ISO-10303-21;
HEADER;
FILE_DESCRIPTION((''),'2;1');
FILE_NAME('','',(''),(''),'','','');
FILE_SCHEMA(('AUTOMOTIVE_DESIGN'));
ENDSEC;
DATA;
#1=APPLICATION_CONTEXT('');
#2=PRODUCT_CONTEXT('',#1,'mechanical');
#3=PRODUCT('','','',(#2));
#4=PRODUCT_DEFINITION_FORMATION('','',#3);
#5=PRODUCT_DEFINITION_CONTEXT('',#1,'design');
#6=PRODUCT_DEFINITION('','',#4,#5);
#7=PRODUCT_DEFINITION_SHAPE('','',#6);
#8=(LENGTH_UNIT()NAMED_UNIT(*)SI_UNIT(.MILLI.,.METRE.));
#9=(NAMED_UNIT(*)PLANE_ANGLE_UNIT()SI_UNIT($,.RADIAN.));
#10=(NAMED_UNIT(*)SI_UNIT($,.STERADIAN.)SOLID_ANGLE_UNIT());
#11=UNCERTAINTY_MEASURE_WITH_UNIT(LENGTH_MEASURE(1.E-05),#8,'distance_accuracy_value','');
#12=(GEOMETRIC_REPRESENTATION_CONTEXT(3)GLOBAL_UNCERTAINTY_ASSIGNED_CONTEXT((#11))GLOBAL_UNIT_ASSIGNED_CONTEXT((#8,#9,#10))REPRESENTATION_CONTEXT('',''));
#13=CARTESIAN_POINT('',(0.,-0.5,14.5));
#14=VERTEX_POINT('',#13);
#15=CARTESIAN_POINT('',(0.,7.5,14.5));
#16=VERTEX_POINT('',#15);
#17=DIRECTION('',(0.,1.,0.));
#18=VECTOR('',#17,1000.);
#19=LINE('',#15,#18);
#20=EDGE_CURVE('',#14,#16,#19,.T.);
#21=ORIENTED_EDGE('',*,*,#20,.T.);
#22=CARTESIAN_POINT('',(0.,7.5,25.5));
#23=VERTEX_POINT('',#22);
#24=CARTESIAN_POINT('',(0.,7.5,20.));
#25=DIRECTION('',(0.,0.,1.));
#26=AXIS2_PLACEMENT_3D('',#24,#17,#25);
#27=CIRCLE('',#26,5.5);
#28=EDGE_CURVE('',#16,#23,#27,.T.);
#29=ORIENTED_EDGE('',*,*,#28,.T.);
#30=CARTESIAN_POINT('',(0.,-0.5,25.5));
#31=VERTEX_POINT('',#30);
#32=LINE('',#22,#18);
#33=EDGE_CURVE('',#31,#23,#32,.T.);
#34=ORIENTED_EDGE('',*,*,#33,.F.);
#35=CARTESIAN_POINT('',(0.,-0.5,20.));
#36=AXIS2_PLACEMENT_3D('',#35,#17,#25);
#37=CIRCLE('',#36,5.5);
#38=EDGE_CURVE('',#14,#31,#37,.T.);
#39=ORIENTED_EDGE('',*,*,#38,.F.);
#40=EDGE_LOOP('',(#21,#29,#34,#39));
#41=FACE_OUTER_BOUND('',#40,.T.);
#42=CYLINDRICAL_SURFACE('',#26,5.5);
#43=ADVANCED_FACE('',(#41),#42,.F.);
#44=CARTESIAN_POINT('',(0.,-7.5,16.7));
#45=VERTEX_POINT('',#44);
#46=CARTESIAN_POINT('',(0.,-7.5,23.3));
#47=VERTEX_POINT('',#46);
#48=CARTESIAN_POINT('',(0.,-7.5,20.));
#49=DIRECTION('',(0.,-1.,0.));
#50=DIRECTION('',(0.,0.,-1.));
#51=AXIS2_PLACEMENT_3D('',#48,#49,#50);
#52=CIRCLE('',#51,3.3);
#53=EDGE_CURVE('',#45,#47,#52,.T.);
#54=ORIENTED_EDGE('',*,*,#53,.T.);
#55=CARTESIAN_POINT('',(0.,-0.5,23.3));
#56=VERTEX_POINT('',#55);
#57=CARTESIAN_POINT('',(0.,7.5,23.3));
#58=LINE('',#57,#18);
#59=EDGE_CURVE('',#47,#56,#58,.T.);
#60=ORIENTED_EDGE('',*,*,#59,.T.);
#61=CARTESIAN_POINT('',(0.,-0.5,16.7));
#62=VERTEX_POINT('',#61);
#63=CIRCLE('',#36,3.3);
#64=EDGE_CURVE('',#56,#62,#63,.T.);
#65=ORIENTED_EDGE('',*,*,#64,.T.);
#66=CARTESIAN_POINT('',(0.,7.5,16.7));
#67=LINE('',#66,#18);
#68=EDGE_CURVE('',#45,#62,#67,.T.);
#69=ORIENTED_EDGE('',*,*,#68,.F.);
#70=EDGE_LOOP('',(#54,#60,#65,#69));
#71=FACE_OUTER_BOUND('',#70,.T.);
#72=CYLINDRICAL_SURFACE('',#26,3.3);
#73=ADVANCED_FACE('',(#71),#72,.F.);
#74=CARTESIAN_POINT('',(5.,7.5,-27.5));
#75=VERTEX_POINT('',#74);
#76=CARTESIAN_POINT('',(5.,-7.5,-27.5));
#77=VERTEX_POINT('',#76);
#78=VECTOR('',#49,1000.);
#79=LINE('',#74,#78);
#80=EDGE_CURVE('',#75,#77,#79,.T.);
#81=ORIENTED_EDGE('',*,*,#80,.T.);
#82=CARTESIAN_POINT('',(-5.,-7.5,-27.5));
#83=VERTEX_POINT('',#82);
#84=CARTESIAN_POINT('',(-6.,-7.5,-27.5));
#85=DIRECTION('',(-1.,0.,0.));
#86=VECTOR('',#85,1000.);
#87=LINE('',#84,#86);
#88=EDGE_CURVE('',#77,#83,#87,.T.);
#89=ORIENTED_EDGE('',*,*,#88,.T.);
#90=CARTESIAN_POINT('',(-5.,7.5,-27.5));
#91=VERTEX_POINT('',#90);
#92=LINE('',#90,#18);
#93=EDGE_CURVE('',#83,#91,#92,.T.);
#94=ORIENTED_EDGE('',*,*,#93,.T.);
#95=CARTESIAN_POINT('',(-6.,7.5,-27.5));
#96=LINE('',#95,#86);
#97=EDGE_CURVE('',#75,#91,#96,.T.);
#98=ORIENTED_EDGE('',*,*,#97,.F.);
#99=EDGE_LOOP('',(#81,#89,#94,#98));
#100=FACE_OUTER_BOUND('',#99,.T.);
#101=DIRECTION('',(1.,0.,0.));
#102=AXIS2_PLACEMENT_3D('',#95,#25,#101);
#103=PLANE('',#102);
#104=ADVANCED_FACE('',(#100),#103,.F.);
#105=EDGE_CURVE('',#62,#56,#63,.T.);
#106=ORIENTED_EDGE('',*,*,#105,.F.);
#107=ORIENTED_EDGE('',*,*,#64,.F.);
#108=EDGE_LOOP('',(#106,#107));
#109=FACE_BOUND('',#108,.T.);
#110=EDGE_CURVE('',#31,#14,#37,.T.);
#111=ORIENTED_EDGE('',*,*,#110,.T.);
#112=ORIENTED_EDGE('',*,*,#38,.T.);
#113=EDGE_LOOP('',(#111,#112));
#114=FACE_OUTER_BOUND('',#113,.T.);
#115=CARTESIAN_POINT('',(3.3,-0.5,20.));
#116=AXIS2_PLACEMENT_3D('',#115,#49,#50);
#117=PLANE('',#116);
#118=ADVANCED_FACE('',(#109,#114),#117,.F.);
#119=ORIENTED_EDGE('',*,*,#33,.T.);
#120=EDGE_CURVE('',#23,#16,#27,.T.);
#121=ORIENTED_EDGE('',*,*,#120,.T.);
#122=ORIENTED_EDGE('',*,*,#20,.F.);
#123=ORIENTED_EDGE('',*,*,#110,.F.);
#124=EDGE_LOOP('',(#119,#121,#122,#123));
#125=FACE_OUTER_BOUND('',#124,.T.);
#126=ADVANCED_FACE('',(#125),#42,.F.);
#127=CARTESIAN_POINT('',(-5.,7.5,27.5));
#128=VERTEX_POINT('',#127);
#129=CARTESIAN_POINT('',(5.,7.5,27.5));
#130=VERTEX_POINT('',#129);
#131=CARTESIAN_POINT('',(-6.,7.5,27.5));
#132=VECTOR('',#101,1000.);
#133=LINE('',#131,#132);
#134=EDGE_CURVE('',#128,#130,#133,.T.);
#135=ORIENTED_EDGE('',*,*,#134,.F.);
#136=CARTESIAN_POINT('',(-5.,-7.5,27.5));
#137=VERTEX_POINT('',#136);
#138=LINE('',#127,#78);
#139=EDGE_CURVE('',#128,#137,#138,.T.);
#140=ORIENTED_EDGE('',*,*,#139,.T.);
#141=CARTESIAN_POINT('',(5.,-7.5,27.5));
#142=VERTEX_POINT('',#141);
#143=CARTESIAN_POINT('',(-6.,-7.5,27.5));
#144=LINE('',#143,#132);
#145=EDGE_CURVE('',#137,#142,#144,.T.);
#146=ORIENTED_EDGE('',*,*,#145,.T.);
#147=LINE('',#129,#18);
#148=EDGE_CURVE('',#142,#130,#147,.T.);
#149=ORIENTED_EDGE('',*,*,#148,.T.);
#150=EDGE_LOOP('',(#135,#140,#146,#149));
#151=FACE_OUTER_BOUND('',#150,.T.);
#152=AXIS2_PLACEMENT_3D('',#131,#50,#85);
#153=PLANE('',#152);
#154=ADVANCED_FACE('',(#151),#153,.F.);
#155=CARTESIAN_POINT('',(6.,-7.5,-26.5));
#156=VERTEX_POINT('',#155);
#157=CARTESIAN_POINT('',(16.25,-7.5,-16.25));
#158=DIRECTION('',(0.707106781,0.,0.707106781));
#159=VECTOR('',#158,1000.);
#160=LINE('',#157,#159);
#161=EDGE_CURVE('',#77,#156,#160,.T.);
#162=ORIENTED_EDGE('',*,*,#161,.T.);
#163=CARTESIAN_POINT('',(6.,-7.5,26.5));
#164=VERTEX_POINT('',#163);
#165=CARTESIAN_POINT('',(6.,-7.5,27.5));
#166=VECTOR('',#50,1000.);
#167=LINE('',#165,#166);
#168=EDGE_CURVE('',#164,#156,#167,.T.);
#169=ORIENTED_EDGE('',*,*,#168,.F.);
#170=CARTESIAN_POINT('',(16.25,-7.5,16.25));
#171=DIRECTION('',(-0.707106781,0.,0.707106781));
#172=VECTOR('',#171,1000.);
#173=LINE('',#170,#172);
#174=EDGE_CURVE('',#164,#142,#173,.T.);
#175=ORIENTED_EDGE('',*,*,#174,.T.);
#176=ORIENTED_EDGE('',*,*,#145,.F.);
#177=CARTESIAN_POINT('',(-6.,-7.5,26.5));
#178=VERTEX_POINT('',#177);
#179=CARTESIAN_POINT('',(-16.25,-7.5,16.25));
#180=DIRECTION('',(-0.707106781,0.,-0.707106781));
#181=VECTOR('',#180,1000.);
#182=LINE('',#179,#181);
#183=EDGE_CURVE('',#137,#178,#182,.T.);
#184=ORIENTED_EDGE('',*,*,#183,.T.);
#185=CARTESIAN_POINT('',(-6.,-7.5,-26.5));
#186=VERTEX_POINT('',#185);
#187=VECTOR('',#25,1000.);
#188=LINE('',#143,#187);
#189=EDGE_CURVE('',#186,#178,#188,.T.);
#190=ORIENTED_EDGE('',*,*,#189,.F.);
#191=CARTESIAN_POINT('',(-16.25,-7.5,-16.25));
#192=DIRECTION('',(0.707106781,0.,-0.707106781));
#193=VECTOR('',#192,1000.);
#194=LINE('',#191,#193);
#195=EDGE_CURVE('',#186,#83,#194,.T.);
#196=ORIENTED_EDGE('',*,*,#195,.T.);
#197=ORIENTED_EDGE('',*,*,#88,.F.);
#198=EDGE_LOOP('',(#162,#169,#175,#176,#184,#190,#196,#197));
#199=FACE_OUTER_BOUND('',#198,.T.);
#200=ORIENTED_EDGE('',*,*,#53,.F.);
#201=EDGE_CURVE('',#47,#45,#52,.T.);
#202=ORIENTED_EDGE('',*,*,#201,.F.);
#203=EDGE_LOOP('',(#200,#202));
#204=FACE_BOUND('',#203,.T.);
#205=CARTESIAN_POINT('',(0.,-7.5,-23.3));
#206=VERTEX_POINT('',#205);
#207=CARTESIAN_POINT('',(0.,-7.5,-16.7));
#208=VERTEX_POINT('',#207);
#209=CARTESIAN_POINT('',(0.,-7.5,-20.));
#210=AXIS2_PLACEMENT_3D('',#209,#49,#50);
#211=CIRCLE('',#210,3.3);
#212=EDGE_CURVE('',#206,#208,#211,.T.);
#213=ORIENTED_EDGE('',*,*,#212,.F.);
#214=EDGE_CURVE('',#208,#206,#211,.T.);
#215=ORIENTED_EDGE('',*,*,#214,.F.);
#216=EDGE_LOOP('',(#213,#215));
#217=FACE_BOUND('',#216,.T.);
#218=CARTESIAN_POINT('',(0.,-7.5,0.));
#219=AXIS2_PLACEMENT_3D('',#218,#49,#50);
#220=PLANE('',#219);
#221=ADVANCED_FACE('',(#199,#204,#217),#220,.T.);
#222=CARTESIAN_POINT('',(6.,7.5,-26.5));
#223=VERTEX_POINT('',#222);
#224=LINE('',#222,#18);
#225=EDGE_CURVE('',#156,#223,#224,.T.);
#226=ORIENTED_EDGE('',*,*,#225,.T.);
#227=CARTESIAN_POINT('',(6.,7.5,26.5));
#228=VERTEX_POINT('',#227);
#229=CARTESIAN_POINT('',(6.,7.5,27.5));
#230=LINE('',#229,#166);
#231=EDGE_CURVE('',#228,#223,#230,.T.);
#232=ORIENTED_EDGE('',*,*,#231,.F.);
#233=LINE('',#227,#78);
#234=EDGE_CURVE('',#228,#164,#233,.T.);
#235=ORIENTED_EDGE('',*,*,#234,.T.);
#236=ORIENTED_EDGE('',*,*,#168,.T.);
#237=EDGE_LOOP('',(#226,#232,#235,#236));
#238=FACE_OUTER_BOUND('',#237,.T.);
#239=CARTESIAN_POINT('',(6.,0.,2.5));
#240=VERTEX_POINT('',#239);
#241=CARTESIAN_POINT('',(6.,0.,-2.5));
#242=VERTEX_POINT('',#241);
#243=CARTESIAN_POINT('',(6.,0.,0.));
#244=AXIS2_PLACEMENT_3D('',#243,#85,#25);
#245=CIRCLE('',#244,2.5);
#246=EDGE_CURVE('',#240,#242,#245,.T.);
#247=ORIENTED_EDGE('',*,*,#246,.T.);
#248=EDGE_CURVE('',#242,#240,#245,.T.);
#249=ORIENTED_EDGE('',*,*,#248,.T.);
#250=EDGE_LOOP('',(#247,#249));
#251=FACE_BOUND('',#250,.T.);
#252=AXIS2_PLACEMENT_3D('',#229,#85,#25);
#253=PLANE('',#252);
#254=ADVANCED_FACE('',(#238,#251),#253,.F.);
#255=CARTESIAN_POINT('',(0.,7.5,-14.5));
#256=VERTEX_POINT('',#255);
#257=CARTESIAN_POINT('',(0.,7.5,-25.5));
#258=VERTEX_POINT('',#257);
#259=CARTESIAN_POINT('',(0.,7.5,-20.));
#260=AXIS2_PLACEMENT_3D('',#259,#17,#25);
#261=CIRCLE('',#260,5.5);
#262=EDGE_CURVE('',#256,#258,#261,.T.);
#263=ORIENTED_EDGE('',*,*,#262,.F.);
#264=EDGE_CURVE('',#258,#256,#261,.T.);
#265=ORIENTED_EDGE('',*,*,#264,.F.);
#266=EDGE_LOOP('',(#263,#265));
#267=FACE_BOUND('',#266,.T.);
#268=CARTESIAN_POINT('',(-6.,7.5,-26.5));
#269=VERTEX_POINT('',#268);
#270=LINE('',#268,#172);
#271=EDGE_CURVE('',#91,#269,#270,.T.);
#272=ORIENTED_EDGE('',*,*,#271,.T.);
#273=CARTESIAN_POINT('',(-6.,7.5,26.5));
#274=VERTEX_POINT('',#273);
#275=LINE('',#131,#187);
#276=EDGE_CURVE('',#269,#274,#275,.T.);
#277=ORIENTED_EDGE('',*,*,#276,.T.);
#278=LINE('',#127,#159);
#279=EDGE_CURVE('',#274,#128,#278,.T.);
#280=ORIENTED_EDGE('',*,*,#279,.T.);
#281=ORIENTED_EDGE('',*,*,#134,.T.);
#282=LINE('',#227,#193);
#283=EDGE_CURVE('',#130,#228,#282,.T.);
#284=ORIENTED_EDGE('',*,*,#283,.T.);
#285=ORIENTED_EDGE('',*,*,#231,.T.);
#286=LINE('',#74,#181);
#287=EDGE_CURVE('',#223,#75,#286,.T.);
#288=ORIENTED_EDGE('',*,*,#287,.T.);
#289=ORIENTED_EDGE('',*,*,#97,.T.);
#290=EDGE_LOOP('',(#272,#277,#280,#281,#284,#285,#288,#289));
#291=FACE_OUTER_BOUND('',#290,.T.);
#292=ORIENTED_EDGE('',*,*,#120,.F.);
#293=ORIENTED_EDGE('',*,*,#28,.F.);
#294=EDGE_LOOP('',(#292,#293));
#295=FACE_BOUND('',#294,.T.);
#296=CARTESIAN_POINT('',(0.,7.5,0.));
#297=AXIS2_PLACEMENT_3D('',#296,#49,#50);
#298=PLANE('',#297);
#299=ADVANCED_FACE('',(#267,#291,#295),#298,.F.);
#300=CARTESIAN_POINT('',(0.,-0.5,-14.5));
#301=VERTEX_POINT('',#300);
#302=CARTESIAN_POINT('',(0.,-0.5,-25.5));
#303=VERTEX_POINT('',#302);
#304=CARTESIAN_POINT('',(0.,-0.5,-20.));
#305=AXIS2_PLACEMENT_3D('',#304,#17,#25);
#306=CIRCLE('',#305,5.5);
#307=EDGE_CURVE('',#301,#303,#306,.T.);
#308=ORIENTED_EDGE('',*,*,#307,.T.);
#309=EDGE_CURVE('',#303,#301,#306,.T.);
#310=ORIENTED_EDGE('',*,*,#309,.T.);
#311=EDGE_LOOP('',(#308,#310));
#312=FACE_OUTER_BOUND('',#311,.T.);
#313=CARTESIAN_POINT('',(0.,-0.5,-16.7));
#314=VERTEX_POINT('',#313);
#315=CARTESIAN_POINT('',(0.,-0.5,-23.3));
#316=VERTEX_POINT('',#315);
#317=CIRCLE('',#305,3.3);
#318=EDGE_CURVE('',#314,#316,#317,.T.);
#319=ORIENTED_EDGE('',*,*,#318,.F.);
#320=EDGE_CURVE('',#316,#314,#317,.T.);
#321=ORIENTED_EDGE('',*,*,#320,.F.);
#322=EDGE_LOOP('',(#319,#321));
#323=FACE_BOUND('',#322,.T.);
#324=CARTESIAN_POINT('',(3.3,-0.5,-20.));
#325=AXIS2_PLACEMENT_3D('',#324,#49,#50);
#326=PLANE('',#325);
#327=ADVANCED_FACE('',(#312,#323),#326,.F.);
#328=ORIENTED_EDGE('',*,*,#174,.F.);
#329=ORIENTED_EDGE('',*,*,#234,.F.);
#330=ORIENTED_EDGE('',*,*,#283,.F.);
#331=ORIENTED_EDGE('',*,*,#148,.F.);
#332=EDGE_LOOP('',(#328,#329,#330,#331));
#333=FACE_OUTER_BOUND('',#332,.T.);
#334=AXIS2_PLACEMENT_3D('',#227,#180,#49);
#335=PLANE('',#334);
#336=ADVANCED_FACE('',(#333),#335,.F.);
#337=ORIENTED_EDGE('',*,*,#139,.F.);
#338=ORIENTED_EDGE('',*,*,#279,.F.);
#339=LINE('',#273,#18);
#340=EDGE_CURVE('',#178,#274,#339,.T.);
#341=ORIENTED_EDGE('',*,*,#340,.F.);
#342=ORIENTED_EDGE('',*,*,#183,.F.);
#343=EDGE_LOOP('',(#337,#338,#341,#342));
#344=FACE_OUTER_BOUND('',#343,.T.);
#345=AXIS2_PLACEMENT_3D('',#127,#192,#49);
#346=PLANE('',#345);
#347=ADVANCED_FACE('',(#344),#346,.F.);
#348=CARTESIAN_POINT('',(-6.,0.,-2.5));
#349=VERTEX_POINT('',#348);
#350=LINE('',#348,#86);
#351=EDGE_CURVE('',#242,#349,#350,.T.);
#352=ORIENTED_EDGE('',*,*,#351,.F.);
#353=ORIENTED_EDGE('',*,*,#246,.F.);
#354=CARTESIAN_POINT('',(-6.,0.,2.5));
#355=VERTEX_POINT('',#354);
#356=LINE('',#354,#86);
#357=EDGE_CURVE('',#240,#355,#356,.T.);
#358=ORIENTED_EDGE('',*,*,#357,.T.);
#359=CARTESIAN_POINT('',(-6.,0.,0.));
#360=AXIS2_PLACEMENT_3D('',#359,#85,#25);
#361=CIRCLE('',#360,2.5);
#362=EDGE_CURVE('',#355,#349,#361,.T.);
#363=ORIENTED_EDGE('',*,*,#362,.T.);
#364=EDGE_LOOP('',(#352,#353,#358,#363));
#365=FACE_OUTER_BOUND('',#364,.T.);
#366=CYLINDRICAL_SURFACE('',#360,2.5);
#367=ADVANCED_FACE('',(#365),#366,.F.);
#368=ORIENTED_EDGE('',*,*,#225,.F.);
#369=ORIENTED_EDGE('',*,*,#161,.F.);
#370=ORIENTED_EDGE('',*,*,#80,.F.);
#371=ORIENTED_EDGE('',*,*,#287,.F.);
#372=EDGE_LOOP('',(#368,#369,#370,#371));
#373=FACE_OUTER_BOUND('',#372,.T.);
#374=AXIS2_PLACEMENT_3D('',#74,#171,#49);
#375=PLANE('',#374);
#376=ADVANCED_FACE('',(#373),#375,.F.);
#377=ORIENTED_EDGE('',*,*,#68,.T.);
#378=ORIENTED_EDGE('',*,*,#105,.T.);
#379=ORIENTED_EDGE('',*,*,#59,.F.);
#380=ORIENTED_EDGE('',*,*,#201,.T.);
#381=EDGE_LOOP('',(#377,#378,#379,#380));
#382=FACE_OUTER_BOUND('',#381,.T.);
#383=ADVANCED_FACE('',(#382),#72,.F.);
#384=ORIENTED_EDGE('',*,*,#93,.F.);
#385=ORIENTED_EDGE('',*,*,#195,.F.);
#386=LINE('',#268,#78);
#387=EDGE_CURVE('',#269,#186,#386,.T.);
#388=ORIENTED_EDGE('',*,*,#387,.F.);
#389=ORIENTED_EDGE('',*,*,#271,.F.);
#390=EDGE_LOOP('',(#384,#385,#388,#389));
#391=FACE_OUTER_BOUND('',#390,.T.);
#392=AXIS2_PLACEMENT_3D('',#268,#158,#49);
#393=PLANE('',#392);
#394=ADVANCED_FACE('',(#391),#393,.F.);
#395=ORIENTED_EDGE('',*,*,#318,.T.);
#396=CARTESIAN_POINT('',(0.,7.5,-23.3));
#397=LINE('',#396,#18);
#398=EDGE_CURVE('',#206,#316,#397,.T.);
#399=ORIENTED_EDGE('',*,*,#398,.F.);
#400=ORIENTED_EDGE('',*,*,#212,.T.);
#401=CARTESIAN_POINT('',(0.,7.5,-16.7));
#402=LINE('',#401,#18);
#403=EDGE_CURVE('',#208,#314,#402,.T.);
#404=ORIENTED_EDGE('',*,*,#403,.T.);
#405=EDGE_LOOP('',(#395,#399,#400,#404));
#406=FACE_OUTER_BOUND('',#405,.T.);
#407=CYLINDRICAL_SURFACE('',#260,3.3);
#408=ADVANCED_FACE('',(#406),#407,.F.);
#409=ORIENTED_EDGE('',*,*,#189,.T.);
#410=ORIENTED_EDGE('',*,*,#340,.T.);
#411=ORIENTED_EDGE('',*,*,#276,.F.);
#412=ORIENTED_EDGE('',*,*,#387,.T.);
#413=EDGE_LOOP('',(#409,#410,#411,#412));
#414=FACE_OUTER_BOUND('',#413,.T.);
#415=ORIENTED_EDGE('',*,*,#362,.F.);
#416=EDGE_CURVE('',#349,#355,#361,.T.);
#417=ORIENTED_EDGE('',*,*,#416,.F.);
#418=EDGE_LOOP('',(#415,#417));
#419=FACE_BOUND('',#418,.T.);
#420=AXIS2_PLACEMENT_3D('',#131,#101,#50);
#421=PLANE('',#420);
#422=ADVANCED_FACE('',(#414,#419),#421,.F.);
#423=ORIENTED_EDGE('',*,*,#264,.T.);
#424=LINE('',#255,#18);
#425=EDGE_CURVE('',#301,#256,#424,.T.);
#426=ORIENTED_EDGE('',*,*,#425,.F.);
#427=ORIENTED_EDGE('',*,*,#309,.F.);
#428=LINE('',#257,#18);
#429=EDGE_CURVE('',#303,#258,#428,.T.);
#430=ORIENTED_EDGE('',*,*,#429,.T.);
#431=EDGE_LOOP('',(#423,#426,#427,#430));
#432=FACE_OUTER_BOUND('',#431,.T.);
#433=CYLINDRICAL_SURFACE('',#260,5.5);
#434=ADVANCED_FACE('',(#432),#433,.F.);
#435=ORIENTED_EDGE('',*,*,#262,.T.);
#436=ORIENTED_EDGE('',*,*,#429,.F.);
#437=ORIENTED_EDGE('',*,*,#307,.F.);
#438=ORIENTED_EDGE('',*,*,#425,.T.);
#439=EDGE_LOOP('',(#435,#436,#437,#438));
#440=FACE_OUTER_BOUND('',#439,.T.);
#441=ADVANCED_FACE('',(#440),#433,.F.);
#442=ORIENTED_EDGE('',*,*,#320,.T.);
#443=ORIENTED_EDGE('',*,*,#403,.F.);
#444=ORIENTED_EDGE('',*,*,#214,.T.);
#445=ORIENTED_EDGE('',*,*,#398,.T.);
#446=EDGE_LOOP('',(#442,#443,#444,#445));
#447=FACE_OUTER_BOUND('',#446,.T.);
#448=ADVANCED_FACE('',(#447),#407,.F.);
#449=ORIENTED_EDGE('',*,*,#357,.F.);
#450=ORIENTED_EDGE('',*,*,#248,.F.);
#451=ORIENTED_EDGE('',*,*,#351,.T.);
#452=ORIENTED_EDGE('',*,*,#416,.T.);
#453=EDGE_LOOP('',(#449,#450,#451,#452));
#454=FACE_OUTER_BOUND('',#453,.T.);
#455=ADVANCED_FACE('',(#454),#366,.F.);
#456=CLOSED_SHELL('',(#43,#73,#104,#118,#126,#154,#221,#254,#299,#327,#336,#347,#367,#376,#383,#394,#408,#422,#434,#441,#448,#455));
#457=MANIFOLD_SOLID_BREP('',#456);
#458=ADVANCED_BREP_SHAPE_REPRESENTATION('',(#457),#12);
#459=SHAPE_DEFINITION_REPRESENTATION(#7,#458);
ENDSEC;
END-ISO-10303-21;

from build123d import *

# Parameters (mm, degrees)
SKETCH_1_W                   = 12
SKETCH_1_H                   = 55
EXTRUDE_1_DEPTH              = 7.5
CHAMFER_1_SIZE               = 1
HOLE_WIZARD_M6_1_D           = 6.6
HOLE_WIZARD_M6_1_CBORE_D     = 11
HOLE_WIZARD_M6_1_CBORE_DEPTH = 8
HOLE_WIZARD_M6_1_2_D         = 5


with BuildPart() as part:
    # 草图1 → 凸台-拉伸1 (new, symmetric)
    with BuildSketch(Plane(origin=(0, 0, 0), x_dir=(1, 0, 0), z_dir=(0, 1, 0))):
        Rectangle(SKETCH_1_W, SKETCH_1_H)
    extrude(amount=EXTRUDE_1_DEPTH, both=True)

    # 倒角1
    chamfer_1_edges = [part.edges().sort_by_distance(p)[0] for p in [
        (6, 0, 27.5),
        (-6, 0, 27.5),
        (-6, 0, -27.5),
        (6, 0, -27.5),
    ]]
    chamfer(chamfer_1_edges, length=CHAMFER_1_SIZE)

    # Hole Wizard M6 _1 (through all)
    with Locations(Plane(origin=(0, 7.5, 0), x_dir=(1, 0, 0), z_dir=(0, 1, 0))):
        with Locations((0, 20), (0, -20)):
            CounterBoreHole(HOLE_WIZARD_M6_1_D / 2, HOLE_WIZARD_M6_1_CBORE_D / 2, HOLE_WIZARD_M6_1_CBORE_DEPTH)

    # Hole Wizard M6 _1 2 (through all)
    with Locations(Plane.ZY.offset(6)):
        with Locations((0, 0)):
            Hole(HOLE_WIZARD_M6_1_2_D / 2)


solid = part.part
